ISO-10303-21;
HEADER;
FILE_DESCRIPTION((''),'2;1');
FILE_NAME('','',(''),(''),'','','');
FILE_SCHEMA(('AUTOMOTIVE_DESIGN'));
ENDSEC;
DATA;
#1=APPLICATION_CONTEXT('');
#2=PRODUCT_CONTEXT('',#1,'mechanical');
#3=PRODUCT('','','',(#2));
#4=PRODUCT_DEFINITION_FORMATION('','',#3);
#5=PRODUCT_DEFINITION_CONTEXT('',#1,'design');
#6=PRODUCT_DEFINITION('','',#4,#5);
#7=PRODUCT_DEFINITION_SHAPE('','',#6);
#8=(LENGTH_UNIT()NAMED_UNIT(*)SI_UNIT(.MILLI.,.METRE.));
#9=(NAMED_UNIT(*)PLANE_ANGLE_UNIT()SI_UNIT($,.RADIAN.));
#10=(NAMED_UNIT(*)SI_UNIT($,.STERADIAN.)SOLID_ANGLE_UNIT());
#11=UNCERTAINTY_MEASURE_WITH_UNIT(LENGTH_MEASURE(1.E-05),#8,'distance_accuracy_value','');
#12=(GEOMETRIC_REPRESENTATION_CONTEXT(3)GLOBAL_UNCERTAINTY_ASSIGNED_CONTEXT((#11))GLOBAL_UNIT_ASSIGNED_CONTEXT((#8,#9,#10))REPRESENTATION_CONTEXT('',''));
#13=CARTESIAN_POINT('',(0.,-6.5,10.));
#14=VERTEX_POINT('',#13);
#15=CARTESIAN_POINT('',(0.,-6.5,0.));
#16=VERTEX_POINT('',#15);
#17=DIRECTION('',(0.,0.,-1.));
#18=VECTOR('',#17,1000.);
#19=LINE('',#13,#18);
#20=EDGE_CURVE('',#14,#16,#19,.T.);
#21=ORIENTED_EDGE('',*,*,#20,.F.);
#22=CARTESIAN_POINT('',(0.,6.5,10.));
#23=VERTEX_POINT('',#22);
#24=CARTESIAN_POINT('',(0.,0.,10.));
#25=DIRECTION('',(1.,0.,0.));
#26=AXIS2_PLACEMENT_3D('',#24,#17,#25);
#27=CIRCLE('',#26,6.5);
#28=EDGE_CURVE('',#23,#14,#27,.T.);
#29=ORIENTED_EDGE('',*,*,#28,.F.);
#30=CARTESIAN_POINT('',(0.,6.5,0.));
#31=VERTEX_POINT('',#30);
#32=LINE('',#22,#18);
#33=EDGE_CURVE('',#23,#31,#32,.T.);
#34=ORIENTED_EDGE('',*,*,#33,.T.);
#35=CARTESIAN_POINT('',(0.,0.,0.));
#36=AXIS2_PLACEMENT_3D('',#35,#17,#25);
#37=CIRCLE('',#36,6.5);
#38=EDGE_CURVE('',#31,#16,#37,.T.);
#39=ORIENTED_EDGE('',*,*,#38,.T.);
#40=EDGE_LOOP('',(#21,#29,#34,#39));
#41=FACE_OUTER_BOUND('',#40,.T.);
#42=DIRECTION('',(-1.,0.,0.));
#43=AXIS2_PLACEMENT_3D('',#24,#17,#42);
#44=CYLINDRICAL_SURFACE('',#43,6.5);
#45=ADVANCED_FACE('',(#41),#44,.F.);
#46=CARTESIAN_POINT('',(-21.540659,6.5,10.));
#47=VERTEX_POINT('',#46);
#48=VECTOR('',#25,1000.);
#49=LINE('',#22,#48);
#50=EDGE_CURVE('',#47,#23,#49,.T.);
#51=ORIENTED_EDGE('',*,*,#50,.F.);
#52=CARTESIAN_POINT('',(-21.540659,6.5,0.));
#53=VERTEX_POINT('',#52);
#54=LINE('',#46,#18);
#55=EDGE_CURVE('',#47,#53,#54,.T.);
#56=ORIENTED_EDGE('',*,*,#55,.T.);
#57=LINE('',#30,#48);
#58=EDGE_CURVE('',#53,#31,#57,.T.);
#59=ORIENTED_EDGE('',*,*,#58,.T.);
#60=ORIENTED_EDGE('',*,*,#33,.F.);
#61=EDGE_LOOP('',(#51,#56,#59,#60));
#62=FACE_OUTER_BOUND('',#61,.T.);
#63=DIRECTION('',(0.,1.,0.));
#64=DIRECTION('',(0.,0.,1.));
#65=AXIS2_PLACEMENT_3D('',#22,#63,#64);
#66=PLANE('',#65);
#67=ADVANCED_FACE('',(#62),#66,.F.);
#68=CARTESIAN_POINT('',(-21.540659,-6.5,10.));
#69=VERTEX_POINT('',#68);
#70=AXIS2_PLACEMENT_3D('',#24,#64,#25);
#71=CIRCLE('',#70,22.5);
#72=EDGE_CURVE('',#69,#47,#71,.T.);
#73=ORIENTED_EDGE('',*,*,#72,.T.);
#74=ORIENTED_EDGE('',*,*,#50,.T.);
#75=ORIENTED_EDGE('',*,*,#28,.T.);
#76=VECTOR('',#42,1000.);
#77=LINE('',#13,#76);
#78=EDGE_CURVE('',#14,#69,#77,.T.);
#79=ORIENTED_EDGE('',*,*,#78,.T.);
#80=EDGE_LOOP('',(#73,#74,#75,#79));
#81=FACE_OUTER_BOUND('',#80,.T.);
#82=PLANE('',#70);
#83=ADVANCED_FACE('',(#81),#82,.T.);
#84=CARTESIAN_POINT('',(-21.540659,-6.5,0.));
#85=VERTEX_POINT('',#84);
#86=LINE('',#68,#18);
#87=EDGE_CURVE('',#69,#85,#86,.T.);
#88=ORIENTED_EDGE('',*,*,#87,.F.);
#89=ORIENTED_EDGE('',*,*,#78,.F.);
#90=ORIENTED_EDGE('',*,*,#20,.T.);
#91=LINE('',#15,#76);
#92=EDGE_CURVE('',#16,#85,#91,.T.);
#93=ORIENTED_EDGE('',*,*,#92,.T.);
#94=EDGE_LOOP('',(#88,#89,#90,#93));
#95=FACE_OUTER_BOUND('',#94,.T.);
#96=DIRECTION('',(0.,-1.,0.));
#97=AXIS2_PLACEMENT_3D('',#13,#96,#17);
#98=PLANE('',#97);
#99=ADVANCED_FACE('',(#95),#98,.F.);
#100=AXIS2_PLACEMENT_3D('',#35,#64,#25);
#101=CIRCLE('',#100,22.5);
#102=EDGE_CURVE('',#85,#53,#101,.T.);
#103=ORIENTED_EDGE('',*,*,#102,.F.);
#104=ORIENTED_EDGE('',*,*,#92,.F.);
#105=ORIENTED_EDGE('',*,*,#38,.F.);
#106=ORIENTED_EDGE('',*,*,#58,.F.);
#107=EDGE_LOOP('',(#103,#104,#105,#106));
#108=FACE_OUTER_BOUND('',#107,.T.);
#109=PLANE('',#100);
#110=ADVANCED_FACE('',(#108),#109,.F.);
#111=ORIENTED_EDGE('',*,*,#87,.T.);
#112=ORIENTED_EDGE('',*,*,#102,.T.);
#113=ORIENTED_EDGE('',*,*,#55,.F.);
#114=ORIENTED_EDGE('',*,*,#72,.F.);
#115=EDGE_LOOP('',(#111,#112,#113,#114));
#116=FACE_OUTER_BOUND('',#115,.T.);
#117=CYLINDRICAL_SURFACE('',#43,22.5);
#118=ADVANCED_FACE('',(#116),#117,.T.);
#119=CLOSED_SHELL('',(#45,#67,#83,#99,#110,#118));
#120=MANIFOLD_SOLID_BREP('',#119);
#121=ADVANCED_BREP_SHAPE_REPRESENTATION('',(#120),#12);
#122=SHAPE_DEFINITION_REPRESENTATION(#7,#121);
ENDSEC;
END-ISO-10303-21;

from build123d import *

# Parameters (mm, degrees)
BOSS_EXTRUDE1_DEPTH = 10


with BuildPart() as part:
    # Sketch1 → Boss-Extrude1 (new body)
    with BuildSketch(Plane.XY):
        with BuildLine():
            Line((0, 6.5), (-21.540659229, 6.5))
            ThreePointArc((-21.540659229, 6.5), (22.5, 0), (-21.540659229, -6.5))
            Line((-21.540659229, -6.5), (0, -6.5))
            ThreePointArc((0, -6.5), (6.5, 0), (0, 6.5))
        make_face()
    extrude(amount=BOSS_EXTRUDE1_DEPTH)


solid = part.part
